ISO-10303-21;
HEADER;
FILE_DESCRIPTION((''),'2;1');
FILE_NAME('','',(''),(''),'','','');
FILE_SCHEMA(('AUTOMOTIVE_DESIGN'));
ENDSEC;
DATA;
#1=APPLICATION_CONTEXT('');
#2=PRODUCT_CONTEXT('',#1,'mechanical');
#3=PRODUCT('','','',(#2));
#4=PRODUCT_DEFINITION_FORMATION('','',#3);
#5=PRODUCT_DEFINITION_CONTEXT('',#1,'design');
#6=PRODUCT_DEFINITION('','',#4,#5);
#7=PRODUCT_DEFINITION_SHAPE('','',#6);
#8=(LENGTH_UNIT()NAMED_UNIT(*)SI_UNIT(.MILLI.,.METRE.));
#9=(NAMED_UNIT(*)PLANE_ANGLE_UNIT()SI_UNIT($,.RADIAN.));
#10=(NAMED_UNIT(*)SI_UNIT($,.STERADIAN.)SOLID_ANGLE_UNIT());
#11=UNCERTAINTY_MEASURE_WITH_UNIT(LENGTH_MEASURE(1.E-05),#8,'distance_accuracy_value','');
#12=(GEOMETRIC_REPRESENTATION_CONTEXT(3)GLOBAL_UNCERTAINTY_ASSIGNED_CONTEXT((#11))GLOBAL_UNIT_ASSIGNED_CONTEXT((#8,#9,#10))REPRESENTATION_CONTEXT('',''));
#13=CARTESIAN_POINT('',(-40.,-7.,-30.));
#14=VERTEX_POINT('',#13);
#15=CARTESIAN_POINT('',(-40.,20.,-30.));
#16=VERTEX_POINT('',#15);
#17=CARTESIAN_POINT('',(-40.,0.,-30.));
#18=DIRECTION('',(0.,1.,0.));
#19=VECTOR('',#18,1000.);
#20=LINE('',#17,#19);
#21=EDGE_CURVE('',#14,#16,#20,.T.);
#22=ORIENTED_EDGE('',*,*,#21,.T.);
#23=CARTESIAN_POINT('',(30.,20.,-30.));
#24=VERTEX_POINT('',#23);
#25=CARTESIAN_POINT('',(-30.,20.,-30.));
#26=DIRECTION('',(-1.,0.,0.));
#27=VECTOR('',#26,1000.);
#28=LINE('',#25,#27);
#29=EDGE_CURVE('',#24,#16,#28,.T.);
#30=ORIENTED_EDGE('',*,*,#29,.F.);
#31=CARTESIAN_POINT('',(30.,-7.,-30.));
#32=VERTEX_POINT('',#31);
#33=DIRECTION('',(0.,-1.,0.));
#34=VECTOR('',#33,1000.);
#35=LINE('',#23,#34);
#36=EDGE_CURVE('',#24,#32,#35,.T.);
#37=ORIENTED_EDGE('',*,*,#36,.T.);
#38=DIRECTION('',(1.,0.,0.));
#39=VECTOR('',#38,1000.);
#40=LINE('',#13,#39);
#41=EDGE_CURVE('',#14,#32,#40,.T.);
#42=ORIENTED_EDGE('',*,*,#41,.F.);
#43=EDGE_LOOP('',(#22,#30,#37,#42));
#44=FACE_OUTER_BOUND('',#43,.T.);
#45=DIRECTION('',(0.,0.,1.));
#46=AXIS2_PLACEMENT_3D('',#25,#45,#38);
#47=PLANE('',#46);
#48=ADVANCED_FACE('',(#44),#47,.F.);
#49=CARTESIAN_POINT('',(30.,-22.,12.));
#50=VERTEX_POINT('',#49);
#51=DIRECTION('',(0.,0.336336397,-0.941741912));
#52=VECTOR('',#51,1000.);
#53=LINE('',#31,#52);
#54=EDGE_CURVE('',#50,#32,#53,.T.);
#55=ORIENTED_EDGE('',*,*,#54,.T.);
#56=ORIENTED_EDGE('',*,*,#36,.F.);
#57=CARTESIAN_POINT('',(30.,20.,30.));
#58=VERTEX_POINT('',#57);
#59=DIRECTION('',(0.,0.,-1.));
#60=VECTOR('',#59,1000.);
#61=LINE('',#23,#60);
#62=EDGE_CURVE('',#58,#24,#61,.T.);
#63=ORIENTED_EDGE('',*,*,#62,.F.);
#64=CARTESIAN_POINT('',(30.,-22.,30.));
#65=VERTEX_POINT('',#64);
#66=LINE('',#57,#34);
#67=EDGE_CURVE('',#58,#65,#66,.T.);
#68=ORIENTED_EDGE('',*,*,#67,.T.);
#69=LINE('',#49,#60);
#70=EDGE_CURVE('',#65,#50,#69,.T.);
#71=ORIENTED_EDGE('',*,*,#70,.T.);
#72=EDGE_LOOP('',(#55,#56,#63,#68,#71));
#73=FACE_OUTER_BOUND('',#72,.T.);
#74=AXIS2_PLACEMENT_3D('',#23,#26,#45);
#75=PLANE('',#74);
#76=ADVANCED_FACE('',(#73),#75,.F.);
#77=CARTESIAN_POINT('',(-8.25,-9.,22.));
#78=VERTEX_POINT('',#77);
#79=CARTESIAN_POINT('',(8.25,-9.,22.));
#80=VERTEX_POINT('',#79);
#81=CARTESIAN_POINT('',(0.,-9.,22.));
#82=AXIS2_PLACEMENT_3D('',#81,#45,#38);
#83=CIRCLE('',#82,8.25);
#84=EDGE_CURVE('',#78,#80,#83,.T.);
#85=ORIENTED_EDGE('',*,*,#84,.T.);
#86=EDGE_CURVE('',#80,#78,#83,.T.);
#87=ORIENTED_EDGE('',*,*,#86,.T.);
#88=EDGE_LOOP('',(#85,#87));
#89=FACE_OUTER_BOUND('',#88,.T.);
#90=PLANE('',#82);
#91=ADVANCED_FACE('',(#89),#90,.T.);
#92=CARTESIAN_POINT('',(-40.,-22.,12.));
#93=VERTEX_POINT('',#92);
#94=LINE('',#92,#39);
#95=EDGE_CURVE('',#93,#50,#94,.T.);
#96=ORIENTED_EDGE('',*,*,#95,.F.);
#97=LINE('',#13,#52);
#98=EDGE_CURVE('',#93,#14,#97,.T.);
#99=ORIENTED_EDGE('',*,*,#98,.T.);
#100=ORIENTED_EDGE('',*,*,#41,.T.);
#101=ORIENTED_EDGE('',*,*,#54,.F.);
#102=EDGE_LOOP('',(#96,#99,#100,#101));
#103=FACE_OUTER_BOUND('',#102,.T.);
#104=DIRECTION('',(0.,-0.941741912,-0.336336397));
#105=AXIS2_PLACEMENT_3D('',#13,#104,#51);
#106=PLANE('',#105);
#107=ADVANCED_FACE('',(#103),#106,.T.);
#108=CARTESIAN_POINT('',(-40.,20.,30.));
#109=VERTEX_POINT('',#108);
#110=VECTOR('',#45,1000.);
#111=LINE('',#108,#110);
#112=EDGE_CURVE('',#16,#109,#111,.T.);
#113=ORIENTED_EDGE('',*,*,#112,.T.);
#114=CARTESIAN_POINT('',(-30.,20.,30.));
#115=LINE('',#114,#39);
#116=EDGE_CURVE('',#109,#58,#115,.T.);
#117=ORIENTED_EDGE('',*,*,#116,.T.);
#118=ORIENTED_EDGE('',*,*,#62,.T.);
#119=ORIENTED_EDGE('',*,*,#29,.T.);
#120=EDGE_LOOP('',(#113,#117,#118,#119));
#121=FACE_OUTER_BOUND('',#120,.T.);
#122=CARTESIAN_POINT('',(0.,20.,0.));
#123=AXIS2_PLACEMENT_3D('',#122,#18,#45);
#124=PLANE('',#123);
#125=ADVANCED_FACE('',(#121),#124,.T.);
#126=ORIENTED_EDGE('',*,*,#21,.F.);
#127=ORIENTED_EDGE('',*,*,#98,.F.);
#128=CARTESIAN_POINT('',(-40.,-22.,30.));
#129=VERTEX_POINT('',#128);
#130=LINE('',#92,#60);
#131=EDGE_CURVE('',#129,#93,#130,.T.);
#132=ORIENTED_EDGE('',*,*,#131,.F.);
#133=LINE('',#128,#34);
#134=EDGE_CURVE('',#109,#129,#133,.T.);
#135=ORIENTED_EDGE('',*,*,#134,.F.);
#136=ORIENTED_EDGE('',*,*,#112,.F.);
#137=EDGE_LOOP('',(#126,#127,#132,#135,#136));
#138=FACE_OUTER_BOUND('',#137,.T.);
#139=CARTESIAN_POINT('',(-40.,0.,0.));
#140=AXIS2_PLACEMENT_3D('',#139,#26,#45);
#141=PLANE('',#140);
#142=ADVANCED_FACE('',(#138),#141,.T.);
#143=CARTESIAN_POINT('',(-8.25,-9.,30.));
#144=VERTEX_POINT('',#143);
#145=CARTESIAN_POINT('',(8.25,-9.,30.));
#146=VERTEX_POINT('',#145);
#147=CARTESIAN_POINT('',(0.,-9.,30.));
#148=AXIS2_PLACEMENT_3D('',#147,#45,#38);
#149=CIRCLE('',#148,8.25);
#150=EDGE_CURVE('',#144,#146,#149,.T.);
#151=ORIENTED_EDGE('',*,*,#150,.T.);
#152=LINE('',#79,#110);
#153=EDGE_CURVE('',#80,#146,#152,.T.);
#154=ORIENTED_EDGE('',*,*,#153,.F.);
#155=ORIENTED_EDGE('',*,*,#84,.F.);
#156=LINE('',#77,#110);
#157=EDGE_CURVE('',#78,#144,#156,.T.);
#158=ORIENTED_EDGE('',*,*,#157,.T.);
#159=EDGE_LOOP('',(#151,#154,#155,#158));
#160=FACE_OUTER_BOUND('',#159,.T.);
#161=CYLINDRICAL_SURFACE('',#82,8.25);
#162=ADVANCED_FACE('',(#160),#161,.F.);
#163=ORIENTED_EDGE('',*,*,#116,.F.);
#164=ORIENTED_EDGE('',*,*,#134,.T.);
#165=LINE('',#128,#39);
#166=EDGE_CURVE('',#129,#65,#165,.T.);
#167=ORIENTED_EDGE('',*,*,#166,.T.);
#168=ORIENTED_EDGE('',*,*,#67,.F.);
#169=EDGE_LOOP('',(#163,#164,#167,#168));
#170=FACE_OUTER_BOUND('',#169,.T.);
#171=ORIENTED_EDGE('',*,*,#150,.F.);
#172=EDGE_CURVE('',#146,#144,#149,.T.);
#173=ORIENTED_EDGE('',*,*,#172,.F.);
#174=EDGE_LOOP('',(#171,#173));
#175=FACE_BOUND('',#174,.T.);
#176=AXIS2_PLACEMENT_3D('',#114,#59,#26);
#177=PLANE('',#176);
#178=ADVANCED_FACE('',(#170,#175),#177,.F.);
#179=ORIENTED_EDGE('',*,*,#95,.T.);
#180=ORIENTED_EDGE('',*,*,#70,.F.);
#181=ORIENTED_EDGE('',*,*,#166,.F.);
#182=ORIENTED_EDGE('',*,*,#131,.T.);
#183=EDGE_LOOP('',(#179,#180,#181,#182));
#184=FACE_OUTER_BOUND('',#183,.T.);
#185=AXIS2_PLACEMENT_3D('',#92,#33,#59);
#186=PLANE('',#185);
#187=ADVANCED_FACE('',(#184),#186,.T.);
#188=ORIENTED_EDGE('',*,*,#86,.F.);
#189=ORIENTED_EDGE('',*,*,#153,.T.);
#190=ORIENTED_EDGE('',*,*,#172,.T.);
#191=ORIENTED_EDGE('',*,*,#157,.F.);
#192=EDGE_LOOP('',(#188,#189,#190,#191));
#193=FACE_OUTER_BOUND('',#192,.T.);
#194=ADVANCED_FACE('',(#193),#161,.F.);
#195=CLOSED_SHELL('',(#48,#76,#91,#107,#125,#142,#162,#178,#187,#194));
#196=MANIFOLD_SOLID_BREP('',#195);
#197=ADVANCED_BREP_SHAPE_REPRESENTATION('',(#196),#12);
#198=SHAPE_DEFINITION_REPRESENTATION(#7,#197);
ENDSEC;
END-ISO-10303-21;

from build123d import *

# Parameters (mm, degrees)
SKETCH1_W           = 60
SKETCH1_H           = 60
BOSS_EXTRUDE1_DEPTH = 20
BOSS_EXTRUDE2_DEPTH = 70
SKETCH8_R           = 8.25
CUT_EXTRUDE5_DEPTH  = 8


with BuildPart() as part:
    # Sketch1 → Boss-Extrude1 (new body)
    with BuildSketch(Plane(origin=(0, 0, 0), x_dir=(1, 0, 0), z_dir=(0, 1, 0))):
        Rectangle(SKETCH1_W, SKETCH1_H)
    extrude(amount=BOSS_EXTRUDE1_DEPTH)

    # Sketch2 → Boss-Extrude2 (add)
    with BuildSketch(Plane(origin=(30, 0, 0), x_dir=(0, 0, -1), z_dir=(1, 0, 0))):
        Polygon((30, 20), (30, 0), (30, -7), (-12, -22), (-30, -22), (-30, 20), align=None)
    extrude(amount=-BOSS_EXTRUDE2_DEPTH)

    # Sketch8 → Cut-Extrude5 (cut)
    with BuildSketch(Plane.XY.offset(30)):
        with Locations((0, -9)):
            Circle(SKETCH8_R)
    extrude(amount=-CUT_EXTRUDE5_DEPTH, mode=Mode.SUBTRACT)


solid = part.part
